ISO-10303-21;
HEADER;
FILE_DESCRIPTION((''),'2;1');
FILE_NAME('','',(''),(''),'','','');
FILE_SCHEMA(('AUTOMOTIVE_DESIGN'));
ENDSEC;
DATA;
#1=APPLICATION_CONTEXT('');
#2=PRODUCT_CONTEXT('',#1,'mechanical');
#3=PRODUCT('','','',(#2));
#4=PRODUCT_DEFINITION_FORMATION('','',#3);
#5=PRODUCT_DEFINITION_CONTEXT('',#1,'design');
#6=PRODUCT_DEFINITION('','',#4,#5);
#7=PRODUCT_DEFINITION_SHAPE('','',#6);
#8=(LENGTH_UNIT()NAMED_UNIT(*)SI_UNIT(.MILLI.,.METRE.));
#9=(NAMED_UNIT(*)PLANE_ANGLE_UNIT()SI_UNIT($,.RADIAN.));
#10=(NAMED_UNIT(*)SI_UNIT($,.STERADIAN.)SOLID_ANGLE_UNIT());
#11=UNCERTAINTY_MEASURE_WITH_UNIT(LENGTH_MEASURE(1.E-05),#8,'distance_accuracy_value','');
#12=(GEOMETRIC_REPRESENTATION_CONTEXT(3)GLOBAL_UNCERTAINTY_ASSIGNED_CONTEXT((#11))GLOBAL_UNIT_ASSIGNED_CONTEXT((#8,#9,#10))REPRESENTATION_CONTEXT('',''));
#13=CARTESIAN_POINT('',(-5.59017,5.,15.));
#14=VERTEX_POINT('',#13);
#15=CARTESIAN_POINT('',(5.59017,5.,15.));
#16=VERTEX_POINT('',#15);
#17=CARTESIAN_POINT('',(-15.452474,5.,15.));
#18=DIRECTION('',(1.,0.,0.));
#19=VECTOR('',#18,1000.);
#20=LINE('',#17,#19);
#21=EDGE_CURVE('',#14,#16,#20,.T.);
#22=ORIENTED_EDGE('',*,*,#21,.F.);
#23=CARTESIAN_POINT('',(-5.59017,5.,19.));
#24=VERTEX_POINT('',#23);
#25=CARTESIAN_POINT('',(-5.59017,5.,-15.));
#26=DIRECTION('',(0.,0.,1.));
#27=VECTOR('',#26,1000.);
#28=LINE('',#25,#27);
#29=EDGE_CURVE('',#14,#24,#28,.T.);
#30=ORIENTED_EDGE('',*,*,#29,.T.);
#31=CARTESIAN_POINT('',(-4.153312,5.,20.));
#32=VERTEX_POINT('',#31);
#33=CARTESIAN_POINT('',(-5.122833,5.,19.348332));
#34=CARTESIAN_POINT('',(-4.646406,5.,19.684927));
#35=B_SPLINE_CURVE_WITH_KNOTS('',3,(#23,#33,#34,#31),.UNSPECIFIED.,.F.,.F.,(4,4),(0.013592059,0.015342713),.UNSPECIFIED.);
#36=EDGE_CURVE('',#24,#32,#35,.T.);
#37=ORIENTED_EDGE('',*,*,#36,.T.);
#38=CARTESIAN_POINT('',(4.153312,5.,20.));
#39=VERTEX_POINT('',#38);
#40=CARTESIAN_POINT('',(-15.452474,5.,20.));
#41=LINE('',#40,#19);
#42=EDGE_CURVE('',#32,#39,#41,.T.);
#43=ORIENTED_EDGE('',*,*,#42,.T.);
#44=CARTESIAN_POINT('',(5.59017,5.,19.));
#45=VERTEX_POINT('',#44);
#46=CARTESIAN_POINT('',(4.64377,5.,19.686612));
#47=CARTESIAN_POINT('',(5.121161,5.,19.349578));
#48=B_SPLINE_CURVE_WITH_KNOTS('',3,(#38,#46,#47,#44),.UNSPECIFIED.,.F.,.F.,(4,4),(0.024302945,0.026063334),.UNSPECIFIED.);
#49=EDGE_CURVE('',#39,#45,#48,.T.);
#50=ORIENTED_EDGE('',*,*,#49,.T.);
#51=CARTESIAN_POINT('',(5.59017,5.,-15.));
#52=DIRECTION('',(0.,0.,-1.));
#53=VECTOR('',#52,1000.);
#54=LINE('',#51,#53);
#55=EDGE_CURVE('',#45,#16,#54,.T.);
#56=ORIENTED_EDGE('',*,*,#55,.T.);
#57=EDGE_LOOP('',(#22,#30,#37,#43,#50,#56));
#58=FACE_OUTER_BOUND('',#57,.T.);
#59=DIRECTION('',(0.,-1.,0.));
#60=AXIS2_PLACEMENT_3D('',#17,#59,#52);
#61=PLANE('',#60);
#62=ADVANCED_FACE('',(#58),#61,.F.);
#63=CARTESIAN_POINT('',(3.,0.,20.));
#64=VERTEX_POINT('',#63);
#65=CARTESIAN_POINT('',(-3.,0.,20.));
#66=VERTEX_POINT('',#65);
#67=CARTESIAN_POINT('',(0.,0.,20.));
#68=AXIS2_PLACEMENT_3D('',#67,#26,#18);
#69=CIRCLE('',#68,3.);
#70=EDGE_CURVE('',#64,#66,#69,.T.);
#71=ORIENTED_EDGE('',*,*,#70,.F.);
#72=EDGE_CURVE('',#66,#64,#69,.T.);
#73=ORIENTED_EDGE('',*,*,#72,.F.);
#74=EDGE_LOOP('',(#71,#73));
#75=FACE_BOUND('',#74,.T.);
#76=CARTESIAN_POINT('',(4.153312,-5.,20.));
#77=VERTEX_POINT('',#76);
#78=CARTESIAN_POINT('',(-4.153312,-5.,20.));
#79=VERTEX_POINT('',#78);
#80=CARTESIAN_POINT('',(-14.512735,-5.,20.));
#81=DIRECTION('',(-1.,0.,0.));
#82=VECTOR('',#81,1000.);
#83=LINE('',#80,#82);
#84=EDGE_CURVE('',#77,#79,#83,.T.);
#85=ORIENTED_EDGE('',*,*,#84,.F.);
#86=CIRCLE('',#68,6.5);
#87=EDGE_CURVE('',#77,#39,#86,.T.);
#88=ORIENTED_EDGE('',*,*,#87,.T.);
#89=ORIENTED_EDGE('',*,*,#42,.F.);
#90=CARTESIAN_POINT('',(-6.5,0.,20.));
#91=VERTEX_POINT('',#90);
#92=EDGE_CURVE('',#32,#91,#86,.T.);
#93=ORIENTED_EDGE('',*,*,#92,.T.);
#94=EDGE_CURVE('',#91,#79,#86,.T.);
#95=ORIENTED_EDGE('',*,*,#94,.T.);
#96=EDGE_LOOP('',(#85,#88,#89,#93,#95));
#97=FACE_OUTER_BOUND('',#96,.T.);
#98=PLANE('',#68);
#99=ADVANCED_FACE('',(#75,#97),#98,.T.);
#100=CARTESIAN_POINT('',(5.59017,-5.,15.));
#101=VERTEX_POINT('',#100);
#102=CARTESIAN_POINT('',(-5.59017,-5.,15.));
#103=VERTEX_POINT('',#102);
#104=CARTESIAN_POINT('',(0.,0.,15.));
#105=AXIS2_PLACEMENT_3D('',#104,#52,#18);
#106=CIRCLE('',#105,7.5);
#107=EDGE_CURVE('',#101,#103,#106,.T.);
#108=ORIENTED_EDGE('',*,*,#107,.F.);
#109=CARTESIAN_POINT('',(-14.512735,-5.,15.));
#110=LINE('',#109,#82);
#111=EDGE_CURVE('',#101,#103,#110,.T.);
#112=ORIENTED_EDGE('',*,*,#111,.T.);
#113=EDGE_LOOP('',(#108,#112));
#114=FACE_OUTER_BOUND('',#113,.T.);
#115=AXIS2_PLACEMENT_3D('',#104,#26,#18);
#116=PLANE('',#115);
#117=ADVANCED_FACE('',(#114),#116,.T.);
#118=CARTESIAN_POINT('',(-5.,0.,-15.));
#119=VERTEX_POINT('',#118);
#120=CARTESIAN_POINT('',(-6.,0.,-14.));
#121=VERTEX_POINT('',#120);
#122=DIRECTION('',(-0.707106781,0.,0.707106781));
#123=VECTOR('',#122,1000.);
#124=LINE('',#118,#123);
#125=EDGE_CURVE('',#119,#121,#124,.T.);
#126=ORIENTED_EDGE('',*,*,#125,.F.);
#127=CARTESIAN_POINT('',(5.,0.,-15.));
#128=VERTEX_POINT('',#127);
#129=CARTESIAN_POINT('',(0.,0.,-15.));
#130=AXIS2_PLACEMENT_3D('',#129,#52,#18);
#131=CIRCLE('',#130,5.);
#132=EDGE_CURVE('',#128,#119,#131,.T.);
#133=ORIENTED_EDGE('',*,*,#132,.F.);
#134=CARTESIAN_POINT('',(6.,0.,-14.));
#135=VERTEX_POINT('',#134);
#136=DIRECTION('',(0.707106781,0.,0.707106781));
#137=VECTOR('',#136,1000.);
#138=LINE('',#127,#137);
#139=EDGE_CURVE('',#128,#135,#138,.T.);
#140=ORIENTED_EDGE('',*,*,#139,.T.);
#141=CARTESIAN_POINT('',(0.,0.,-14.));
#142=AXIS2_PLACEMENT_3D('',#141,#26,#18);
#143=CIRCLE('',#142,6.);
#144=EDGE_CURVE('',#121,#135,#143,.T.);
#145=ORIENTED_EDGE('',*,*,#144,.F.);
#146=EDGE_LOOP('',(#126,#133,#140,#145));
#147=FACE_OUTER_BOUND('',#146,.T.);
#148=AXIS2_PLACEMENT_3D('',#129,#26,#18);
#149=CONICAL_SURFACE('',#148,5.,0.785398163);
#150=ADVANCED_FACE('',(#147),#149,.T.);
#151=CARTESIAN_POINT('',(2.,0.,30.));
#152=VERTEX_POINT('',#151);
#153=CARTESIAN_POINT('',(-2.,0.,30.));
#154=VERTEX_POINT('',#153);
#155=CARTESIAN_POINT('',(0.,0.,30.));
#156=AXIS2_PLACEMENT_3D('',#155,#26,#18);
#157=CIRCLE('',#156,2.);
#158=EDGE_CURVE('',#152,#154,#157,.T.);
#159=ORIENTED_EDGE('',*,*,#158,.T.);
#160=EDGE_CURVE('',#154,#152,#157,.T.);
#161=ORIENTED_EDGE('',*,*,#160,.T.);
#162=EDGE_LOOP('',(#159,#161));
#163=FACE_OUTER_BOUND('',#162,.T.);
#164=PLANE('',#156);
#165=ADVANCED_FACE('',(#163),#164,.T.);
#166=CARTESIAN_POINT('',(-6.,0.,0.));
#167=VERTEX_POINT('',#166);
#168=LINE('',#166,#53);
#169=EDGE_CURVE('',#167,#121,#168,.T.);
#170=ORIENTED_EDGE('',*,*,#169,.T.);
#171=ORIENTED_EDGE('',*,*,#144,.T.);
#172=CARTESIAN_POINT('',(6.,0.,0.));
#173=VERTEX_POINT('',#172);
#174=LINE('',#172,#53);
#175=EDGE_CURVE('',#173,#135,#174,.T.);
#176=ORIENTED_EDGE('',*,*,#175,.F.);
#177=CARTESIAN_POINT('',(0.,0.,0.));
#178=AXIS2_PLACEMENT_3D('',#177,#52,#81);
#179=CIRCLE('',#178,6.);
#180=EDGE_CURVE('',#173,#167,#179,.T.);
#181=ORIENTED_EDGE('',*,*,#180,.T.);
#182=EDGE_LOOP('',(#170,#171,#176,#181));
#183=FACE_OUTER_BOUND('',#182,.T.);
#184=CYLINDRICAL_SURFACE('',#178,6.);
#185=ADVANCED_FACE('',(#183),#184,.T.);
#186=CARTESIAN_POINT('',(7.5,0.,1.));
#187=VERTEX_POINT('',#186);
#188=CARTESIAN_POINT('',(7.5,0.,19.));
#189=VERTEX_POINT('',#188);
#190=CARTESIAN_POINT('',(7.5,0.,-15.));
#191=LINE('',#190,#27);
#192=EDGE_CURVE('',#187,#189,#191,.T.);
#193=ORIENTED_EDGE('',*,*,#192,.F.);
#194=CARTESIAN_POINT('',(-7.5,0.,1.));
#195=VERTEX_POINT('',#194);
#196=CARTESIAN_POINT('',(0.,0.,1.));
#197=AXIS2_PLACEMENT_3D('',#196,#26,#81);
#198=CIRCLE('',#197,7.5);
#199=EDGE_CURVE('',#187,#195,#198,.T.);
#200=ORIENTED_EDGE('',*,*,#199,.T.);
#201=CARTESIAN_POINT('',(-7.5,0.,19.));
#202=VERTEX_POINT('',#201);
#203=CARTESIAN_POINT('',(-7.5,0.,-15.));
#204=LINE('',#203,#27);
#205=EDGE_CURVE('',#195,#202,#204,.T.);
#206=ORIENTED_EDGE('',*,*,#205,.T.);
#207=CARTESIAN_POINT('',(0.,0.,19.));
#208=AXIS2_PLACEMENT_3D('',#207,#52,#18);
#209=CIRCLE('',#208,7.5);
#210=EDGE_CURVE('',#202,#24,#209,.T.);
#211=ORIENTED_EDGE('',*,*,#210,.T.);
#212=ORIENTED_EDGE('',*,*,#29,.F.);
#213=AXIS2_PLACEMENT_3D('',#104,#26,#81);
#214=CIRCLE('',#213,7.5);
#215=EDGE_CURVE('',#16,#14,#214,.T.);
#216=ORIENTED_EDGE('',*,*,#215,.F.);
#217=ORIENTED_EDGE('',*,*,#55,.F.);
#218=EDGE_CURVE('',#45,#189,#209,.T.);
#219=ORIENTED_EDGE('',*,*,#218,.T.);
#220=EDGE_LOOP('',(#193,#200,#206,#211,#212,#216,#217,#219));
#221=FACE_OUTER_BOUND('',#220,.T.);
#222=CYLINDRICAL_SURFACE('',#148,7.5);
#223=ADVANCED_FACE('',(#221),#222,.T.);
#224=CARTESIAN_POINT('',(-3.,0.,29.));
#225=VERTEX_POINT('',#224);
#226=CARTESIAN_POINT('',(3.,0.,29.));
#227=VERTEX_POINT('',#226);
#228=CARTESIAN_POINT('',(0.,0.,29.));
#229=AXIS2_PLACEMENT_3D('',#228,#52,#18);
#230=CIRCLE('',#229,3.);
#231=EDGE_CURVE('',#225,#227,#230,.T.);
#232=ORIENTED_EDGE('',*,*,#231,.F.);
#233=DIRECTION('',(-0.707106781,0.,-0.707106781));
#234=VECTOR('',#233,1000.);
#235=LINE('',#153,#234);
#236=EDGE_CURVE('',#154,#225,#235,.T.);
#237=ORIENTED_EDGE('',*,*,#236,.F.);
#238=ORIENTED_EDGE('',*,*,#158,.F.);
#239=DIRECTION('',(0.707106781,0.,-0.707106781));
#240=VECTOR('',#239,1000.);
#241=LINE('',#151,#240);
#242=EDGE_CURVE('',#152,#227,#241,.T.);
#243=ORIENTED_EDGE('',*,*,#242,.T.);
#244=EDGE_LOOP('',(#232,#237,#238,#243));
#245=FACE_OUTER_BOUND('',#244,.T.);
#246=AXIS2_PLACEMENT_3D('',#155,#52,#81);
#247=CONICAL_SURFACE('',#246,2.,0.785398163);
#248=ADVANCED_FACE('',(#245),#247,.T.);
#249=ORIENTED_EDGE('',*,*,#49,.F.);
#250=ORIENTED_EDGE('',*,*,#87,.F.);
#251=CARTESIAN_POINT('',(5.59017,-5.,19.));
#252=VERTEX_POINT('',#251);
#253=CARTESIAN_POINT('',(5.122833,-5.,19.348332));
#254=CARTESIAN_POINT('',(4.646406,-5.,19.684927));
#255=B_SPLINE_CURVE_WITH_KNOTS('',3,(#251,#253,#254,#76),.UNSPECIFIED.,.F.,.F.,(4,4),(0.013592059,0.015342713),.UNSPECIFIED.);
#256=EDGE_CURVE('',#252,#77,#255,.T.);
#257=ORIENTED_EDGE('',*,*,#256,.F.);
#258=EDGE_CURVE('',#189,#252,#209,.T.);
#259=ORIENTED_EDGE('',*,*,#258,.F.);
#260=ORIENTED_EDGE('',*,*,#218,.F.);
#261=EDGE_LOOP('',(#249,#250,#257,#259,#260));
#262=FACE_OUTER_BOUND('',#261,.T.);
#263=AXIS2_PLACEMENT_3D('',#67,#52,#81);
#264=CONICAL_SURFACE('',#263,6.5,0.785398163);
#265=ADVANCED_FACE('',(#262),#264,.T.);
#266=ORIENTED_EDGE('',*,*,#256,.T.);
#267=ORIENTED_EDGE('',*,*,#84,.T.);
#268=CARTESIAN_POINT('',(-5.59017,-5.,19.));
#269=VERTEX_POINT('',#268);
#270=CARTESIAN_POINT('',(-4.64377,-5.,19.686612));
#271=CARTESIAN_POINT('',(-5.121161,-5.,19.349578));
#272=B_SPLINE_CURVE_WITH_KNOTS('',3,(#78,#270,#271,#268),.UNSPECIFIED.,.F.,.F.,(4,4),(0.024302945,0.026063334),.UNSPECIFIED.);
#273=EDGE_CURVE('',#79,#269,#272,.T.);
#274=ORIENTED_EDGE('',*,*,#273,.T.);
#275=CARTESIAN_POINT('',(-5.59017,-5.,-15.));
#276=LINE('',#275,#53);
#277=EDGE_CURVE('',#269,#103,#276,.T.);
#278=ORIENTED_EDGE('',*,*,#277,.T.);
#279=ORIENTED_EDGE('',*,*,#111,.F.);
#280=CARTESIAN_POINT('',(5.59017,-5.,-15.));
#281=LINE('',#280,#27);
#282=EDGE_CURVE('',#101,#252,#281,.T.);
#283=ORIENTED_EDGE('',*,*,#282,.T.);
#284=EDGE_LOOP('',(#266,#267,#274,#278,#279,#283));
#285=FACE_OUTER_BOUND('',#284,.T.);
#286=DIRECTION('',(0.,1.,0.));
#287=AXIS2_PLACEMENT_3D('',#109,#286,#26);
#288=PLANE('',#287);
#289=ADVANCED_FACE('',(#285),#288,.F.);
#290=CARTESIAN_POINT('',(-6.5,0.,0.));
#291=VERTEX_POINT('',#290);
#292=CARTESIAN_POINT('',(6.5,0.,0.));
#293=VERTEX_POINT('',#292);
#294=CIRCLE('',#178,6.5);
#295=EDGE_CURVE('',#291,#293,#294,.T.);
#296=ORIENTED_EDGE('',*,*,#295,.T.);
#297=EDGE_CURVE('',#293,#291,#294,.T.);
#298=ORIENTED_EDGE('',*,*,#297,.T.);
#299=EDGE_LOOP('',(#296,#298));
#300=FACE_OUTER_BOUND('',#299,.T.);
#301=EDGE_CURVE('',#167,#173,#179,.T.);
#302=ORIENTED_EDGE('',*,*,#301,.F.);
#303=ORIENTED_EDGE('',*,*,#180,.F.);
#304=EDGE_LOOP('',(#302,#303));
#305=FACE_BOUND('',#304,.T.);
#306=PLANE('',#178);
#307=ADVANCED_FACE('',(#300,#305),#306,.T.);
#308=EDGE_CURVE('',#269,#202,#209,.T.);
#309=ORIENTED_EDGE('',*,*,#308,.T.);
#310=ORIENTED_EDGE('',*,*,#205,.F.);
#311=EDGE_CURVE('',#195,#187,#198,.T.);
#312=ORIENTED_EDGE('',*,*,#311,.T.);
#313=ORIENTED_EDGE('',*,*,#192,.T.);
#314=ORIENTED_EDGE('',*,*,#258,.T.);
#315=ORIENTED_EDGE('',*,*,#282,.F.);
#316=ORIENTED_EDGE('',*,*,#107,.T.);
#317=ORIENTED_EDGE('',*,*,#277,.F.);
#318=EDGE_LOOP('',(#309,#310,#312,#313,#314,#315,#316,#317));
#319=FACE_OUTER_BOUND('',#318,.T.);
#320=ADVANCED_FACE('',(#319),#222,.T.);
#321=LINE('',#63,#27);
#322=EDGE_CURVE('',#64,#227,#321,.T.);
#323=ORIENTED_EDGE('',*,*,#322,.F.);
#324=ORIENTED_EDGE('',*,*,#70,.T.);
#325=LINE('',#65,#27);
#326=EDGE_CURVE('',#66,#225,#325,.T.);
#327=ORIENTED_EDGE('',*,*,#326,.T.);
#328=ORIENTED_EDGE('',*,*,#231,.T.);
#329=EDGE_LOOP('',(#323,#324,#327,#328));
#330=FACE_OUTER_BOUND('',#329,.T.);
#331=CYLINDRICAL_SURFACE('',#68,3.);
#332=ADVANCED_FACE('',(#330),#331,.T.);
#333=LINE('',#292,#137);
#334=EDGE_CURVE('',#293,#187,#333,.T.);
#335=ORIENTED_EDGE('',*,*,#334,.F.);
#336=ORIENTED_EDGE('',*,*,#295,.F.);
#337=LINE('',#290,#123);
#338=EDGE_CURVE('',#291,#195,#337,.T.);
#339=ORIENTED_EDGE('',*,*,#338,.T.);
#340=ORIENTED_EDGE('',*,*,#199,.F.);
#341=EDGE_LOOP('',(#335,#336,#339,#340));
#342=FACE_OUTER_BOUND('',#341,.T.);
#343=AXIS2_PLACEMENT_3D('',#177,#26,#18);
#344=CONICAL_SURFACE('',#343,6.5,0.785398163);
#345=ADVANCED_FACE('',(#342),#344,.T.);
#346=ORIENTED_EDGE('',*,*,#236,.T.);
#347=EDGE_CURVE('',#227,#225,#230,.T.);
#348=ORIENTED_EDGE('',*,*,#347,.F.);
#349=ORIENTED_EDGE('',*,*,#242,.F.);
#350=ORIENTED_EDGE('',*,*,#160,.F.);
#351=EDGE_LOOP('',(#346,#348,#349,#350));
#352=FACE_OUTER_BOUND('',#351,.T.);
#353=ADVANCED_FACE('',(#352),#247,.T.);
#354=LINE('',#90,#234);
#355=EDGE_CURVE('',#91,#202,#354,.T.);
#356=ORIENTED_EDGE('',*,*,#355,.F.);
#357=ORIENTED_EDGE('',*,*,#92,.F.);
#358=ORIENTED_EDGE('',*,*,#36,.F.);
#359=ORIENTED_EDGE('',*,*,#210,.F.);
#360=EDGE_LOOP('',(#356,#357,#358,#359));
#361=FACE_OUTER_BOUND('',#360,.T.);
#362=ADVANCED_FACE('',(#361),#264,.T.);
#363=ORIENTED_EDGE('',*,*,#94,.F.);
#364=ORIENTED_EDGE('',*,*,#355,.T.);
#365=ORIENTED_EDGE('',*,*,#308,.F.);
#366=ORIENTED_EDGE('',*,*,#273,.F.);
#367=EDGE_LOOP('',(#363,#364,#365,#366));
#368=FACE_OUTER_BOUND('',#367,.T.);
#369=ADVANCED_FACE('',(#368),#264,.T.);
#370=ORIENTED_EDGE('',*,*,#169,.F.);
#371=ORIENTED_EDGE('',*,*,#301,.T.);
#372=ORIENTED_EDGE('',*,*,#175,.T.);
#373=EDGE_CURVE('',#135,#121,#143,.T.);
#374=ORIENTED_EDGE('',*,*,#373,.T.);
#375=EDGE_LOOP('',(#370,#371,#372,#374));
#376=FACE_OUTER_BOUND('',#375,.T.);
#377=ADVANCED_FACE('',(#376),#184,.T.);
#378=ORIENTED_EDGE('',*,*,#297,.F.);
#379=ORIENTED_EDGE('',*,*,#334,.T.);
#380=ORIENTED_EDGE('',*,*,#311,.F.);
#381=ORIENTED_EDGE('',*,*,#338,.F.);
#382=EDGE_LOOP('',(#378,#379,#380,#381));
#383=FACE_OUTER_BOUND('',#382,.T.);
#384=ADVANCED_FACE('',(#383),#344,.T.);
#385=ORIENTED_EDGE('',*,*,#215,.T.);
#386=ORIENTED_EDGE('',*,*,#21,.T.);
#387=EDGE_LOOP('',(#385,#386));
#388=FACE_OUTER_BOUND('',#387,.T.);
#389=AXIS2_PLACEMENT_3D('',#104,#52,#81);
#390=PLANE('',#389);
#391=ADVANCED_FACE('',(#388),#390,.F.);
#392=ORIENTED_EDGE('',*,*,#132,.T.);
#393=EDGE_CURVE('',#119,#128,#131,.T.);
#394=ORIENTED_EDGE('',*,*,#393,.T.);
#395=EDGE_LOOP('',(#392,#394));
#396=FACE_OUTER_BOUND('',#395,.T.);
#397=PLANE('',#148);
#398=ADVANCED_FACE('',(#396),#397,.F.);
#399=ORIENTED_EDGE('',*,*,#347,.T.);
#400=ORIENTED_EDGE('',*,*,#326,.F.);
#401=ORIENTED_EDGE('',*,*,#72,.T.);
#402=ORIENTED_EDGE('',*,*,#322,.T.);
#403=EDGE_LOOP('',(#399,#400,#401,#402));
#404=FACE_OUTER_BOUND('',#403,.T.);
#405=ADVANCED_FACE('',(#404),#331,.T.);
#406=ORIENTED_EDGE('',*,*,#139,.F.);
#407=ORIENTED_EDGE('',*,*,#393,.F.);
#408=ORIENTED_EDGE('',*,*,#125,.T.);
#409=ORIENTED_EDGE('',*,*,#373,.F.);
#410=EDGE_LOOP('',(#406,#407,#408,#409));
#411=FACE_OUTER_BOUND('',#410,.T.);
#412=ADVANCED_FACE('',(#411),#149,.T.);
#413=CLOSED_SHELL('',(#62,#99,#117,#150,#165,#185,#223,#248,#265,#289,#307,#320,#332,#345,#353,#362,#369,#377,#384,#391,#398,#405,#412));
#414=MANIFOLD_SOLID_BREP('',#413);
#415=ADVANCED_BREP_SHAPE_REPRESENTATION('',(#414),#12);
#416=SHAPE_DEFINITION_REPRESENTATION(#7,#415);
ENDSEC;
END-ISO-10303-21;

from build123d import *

# Parameters (mm, degrees)
EXTRUDE_1_DEPTH      = 30
EXTRUDE_1_DEPTH_BACK = 15
SKETCH_1_R           = 7.5
SKETCH_2_R           = 7.5
SKETCH_2_R_2         = 3
CUT_EXTRUDE_1_DEPTH  = 10
CHAMFER_1_SIZE       = 1
SKETCH_3_R           = 7.5
SKETCH_3_R_2         = 6
CUT_EXTRUDE_2_DEPTH  = 15
CHAMFER_2_SIZE       = 1
CHAMFER_3_SIZE       = 1
CHAMFER_4_SIZE       = 1
SKETCH_4_W           = 26.213765936
SKETCH_4_H           = 7.269713565
SKETCH_4_W_2         = 30.615700216
SKETCH_4_H_2         = 9.339731857
CUT_EXTRUDE_3_DEPTH  = 5


with BuildPart() as part:
    # 草图1 → 凸台-拉伸1 (new, two sides: drawn at the far end of the back side and taken through both)
    with BuildSketch(Plane.XY.offset(-EXTRUDE_1_DEPTH_BACK)):
        Circle(SKETCH_1_R)
    extrude(amount=EXTRUDE_1_DEPTH + EXTRUDE_1_DEPTH_BACK)

    # 草图2 → 切除-拉伸1 (cut)
    with BuildSketch(Plane.XY.offset(30)):
        Circle(SKETCH_2_R)
        Circle(SKETCH_2_R_2, mode=Mode.SUBTRACT)
    extrude(amount=-CUT_EXTRUDE_1_DEPTH, mode=Mode.SUBTRACT)

    # 倒角1
    chamfer_1_edges = [part.edges().sort_by_distance(p)[0] for p in [
        (-3, 0, 30),
    ]]
    chamfer(chamfer_1_edges, length=CHAMFER_1_SIZE)

    # 草图3 → 切除-拉伸2 (cut)
    with BuildSketch(Plane(origin=(0, 0, -15), x_dir=(-1, 0, 0), z_dir=(0, 0, -1))):
        with Locations(Location((0, 0, 0), (0, 0, 180))):
            Circle(SKETCH_3_R)
        Circle(SKETCH_3_R_2, mode=Mode.SUBTRACT)
    extrude(amount=-CUT_EXTRUDE_2_DEPTH, mode=Mode.SUBTRACT)

    # 倒角2
    chamfer_2_edges = [part.edges().sort_by_distance(p)[0] for p in [
        (6, 0, -15),
    ]]
    chamfer(chamfer_2_edges, length=CHAMFER_2_SIZE)

    # 倒角3
    chamfer_3_edges = [part.edges().sort_by_distance(p)[0] for p in [
        (-7.5, 0, 0),
    ]]
    chamfer(chamfer_3_edges, length=CHAMFER_3_SIZE)

    # 倒角4
    chamfer_4_edges = [part.edges().sort_by_distance(p)[0] for p in [
        (-7.5, 0, 20),
    ]]
    chamfer(chamfer_4_edges, length=CHAMFER_4_SIZE)

    # 草图4 → 切除-拉伸3 (cut)
    with BuildSketch(Plane.XY.offset(20)):
        with Locations((-1.405852491, -8.634856782)):
            Rectangle(SKETCH_4_W, SKETCH_4_H)
        with Locations((-0.14462413, 9.669865929)):
            Rectangle(SKETCH_4_W_2, SKETCH_4_H_2)
    extrude(amount=-CUT_EXTRUDE_3_DEPTH, mode=Mode.SUBTRACT)


solid = part.part
